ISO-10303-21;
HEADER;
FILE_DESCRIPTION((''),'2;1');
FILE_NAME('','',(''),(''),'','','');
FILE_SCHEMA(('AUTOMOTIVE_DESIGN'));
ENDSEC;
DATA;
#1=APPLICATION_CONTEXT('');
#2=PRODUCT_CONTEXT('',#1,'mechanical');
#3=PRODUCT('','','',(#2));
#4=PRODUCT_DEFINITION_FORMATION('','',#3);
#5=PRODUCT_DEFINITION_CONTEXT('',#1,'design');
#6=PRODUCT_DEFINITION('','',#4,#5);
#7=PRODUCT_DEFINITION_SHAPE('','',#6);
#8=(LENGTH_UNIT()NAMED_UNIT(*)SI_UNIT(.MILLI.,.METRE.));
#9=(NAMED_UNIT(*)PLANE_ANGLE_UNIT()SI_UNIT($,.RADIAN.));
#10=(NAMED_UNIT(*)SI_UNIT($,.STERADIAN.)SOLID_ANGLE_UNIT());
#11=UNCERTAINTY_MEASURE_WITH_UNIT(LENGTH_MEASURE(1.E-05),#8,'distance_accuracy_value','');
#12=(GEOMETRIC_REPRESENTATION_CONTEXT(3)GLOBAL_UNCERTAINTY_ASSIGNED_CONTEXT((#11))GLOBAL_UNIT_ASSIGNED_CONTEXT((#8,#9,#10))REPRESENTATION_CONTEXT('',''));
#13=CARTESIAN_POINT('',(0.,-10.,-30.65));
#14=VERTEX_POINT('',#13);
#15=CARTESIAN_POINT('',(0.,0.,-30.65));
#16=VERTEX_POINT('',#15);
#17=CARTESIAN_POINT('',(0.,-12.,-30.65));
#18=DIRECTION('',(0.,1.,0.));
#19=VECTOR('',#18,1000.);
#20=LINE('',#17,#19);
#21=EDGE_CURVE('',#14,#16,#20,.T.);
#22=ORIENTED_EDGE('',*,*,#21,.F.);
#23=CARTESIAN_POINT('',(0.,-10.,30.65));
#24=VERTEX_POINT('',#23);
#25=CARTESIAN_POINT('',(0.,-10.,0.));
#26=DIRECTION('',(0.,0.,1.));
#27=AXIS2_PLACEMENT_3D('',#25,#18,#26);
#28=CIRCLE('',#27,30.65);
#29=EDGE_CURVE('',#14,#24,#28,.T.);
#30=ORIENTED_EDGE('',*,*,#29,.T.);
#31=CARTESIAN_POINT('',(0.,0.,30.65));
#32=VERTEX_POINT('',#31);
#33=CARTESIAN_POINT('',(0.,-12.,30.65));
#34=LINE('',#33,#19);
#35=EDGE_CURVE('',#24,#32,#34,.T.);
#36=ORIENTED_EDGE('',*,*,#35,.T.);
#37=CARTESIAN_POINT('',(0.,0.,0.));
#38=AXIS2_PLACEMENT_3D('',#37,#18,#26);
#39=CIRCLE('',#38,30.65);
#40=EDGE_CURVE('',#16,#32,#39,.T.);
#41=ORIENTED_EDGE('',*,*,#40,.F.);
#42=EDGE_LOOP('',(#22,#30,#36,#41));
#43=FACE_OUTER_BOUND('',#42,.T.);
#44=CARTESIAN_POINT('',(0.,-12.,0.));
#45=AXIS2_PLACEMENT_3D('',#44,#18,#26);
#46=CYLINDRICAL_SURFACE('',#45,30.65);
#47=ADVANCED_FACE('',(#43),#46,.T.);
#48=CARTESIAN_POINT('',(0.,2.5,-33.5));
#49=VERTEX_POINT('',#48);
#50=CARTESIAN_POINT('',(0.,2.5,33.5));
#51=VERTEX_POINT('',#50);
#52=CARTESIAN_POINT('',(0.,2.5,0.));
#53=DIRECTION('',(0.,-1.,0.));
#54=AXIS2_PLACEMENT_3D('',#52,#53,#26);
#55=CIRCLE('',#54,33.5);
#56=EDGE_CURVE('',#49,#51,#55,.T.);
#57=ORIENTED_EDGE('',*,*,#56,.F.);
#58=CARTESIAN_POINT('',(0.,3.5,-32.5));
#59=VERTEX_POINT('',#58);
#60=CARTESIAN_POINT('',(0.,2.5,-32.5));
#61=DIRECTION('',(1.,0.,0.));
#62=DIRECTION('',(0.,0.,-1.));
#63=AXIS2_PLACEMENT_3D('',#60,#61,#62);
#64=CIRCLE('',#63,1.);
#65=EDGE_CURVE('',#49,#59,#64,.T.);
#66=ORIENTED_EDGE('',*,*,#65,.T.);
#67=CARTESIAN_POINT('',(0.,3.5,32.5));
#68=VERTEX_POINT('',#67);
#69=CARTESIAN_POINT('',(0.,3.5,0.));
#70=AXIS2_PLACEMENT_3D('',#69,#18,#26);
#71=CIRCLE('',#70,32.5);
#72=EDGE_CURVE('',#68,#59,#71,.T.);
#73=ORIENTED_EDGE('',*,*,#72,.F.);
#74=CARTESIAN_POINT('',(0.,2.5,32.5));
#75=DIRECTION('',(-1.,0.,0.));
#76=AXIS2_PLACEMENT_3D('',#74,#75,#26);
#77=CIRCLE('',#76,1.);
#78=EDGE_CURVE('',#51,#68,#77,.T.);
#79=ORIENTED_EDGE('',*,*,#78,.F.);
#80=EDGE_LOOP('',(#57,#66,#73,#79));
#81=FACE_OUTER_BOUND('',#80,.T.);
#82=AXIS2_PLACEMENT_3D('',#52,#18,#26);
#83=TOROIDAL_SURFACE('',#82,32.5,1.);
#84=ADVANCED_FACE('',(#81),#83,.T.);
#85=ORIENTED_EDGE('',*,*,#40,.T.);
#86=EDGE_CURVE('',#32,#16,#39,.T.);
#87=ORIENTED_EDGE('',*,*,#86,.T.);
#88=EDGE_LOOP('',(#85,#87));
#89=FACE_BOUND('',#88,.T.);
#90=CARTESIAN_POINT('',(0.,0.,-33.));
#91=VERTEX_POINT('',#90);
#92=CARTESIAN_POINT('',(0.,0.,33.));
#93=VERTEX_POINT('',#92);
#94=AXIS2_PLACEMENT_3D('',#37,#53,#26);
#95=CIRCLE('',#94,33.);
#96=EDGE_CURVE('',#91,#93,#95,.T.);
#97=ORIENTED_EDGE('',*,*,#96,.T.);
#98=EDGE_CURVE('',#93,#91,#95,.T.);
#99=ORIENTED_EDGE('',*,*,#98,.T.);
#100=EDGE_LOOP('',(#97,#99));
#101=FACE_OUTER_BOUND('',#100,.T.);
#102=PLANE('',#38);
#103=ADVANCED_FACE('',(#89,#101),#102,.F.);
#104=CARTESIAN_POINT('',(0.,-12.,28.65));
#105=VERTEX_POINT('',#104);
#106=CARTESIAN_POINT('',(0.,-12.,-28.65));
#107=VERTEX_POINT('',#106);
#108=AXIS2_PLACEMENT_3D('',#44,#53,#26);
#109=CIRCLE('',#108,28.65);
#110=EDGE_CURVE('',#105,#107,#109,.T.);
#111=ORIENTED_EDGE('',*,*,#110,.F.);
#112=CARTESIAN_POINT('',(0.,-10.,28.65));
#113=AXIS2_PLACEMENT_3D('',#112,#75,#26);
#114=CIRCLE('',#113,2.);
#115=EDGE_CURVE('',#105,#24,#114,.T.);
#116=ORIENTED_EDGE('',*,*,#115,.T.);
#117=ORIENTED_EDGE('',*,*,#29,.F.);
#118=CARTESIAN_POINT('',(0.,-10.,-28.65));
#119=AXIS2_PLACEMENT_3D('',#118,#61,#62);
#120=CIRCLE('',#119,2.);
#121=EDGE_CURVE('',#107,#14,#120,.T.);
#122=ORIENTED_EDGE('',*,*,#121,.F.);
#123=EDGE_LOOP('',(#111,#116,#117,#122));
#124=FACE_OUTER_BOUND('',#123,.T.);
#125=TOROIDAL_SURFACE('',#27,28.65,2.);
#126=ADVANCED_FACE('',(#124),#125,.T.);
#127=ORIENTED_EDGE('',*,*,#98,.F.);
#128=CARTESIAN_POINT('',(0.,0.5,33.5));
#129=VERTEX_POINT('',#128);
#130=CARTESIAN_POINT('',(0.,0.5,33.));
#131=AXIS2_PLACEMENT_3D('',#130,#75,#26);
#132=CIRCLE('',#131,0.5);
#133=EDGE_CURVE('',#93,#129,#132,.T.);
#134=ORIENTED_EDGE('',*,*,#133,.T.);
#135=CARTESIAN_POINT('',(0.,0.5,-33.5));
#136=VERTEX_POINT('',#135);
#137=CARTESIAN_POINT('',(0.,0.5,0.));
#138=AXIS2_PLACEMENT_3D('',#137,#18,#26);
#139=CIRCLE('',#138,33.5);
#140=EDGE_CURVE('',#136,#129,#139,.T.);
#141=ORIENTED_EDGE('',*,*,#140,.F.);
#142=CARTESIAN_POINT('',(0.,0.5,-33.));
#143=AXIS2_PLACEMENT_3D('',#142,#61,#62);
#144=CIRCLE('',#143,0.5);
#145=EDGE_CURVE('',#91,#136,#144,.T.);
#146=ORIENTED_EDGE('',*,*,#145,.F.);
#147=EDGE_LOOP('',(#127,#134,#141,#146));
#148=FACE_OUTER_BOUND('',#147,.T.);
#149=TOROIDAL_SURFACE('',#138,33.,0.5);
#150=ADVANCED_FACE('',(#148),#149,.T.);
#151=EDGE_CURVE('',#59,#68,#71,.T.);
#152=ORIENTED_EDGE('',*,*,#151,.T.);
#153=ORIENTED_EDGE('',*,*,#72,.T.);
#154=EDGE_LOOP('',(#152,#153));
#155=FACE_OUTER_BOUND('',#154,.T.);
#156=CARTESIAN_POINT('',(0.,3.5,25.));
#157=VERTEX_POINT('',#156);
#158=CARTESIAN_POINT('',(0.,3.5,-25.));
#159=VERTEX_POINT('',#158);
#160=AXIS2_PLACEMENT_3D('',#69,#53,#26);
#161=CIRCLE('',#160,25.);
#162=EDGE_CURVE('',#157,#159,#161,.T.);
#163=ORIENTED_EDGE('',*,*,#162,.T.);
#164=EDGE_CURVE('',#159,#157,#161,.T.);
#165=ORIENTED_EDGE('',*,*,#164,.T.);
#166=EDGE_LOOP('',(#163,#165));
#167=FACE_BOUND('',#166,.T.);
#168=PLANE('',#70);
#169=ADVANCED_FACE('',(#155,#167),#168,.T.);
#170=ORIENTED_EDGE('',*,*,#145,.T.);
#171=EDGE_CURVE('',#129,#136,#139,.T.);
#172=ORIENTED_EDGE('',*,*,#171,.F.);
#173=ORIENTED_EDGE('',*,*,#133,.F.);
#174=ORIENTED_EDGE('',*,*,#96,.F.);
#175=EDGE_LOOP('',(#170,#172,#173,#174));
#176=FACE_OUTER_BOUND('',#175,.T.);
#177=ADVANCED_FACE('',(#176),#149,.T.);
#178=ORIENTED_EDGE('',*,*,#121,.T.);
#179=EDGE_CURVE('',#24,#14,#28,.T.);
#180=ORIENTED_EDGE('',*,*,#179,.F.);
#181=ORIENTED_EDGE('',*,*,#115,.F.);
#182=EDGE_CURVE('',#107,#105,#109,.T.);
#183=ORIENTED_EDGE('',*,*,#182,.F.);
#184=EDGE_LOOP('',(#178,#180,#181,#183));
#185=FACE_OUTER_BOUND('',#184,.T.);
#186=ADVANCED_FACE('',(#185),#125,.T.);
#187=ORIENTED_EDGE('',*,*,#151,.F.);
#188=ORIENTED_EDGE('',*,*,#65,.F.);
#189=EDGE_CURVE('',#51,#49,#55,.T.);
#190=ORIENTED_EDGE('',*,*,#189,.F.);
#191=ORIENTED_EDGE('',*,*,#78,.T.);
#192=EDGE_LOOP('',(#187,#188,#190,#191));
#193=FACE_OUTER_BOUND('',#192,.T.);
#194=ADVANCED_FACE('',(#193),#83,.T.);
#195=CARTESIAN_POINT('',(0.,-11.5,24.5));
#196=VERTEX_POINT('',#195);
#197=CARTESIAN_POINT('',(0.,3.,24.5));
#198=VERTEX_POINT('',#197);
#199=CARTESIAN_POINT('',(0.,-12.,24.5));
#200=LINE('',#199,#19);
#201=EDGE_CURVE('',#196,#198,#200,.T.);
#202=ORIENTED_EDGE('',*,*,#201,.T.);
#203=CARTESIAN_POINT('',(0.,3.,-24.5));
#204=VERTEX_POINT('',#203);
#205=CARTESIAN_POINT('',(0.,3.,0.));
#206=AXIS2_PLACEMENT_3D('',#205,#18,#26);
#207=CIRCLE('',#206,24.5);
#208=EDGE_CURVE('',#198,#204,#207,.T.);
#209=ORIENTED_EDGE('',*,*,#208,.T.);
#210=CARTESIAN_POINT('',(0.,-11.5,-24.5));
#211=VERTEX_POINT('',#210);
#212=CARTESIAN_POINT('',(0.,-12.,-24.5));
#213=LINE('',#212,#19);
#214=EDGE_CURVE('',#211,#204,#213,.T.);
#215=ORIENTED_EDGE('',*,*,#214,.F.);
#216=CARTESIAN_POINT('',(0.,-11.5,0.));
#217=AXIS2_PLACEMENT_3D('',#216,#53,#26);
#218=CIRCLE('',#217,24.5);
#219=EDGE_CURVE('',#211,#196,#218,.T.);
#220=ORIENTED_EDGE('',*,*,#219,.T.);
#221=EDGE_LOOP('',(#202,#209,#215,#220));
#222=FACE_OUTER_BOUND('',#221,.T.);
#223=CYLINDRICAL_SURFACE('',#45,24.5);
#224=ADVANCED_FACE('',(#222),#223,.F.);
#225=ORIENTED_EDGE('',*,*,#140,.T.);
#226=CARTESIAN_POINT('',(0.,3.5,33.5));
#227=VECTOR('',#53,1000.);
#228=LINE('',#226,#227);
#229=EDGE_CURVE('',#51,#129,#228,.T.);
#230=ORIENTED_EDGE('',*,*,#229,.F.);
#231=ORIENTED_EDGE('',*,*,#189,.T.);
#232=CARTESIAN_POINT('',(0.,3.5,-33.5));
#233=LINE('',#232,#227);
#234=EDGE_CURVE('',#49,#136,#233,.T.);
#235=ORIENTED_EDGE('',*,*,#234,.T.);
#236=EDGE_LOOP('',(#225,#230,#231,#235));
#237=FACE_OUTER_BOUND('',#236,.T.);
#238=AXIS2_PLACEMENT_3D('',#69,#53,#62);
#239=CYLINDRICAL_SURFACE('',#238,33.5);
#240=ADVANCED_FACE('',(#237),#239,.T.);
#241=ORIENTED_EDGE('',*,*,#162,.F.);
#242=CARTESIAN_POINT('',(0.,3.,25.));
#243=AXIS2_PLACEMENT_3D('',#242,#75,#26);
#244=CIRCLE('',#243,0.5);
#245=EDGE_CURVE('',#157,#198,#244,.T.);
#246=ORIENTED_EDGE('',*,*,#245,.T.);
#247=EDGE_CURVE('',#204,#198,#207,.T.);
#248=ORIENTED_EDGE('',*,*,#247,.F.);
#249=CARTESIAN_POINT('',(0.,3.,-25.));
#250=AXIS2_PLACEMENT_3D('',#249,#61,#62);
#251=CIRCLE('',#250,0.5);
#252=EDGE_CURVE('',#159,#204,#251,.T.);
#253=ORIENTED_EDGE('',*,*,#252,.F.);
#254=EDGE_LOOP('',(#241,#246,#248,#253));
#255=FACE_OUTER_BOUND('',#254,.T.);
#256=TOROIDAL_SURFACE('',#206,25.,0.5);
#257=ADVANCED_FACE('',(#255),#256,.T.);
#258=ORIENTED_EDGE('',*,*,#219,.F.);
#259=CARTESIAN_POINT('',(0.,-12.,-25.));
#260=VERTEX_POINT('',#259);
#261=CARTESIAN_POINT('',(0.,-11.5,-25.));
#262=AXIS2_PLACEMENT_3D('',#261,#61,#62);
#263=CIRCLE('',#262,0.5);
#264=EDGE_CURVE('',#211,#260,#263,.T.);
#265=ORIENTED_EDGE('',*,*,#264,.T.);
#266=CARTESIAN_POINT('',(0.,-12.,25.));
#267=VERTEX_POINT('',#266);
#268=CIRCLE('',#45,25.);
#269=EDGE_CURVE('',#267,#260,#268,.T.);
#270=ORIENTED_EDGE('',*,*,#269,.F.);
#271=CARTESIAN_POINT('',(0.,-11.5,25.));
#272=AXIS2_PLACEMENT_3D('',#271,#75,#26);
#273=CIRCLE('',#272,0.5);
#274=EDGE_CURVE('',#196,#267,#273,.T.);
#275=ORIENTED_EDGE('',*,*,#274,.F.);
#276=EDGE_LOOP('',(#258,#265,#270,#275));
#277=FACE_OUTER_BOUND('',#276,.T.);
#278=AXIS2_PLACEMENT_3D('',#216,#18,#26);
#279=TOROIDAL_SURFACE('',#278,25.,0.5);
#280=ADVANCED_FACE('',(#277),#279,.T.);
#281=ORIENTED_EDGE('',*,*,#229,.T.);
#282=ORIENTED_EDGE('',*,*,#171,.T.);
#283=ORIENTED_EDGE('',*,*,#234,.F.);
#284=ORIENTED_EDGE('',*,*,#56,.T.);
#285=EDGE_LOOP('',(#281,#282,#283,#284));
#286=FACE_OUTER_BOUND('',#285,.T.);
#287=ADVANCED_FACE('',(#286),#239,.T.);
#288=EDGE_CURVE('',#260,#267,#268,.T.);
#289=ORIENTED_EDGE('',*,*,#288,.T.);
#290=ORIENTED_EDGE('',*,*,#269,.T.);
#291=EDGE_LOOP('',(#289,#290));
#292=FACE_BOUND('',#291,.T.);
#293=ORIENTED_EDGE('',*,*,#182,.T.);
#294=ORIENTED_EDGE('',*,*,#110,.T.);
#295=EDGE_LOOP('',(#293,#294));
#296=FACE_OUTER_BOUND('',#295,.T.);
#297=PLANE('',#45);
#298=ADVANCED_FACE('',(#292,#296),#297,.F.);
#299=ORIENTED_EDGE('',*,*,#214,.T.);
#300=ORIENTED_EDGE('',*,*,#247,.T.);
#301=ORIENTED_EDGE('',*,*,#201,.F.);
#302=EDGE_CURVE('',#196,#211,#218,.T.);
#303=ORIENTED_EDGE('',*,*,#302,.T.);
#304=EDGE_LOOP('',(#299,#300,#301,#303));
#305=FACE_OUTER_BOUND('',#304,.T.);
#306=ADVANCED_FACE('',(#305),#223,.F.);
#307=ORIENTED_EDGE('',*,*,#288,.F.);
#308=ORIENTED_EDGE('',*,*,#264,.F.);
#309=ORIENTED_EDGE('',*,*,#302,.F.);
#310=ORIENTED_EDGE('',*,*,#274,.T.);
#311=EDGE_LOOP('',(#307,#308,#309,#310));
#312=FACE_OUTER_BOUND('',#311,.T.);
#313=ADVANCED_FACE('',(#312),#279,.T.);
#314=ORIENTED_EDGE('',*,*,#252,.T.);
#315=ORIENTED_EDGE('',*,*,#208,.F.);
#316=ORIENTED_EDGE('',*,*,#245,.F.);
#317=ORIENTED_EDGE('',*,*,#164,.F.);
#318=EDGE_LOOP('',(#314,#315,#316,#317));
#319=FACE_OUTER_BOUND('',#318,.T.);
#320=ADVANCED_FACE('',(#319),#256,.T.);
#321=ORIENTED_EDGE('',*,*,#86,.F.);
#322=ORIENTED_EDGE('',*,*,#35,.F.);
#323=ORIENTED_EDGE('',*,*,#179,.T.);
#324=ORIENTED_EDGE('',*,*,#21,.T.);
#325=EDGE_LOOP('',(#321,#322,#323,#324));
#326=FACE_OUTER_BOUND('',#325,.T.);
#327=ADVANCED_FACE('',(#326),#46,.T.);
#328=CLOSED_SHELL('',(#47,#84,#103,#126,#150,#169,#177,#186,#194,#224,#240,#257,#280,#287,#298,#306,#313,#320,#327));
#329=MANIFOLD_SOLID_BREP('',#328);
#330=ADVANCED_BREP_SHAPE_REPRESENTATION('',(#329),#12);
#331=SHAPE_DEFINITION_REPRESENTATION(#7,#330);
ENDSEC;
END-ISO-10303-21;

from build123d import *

# Parameters (mm, degrees)
SKETCH1_R           = 30.65
BOSS_EXTRUDE1_DEPTH = 12
SKETCH2_R           = 33.5
BOSS_EXTRUDE2_DEPTH = 3.5
SKETCH3_R           = 24.5
CUT_EXTRUDE1_DEPTH  = 50.847266725
FILLET1_R           = 1
FILLET2_R           = 2
FILLET3_R           = 0.5


with BuildPart() as part:
    # Sketch1 → Boss-Extrude1 (new body)
    with BuildSketch(Plane(origin=(0, 0, 0), x_dir=(1, 0, 0), z_dir=(0, 1, 0))):
        with Locations(Location((0, 0, 0), (0, 0, 270))):
            Circle(SKETCH1_R)
    extrude(amount=-BOSS_EXTRUDE1_DEPTH)

    # Sketch2 → Boss-Extrude2 (add)
    with BuildSketch(Plane(origin=(0, 0, 0), x_dir=(1, 0, 0), z_dir=(0, 1, 0))):
        with Locations(Location((0, 0, 0), (0, 0, 270))):
            Circle(SKETCH2_R)
    extrude(amount=BOSS_EXTRUDE2_DEPTH)

    # Sketch3 → Cut-Extrude1 (cut, through all)
    with BuildSketch(Plane(origin=(0, 3.5, 0), x_dir=(1, 0, 0), z_dir=(0, 1, 0))):
        with Locations(Location((0, 0, 0), (0, 0, 270))):
            Circle(SKETCH3_R)
    extrude(amount=-CUT_EXTRUDE1_DEPTH, mode=Mode.SUBTRACT)

    # Fillet1
    fillet1_edges = [part.edges().sort_by_distance(p)[0] for p in [
        (0, 3.5, -33.5),
    ]]
    fillet(fillet1_edges, radius=FILLET1_R)

    # Fillet2
    fillet2_edges = [part.edges().sort_by_distance(p)[0] for p in [
        (0, -12, -30.65),
    ]]
    fillet(fillet2_edges, radius=FILLET2_R)

    # Fillet3
    fillet3_edges = [part.edges().sort_by_distance(p)[0] for p in [
        (0, -12, -24.5),
        (0, 3.5, -24.5),
        (0, 0, -33.5),
    ]]
    fillet(fillet3_edges, radius=FILLET3_R)


solid = part.part
